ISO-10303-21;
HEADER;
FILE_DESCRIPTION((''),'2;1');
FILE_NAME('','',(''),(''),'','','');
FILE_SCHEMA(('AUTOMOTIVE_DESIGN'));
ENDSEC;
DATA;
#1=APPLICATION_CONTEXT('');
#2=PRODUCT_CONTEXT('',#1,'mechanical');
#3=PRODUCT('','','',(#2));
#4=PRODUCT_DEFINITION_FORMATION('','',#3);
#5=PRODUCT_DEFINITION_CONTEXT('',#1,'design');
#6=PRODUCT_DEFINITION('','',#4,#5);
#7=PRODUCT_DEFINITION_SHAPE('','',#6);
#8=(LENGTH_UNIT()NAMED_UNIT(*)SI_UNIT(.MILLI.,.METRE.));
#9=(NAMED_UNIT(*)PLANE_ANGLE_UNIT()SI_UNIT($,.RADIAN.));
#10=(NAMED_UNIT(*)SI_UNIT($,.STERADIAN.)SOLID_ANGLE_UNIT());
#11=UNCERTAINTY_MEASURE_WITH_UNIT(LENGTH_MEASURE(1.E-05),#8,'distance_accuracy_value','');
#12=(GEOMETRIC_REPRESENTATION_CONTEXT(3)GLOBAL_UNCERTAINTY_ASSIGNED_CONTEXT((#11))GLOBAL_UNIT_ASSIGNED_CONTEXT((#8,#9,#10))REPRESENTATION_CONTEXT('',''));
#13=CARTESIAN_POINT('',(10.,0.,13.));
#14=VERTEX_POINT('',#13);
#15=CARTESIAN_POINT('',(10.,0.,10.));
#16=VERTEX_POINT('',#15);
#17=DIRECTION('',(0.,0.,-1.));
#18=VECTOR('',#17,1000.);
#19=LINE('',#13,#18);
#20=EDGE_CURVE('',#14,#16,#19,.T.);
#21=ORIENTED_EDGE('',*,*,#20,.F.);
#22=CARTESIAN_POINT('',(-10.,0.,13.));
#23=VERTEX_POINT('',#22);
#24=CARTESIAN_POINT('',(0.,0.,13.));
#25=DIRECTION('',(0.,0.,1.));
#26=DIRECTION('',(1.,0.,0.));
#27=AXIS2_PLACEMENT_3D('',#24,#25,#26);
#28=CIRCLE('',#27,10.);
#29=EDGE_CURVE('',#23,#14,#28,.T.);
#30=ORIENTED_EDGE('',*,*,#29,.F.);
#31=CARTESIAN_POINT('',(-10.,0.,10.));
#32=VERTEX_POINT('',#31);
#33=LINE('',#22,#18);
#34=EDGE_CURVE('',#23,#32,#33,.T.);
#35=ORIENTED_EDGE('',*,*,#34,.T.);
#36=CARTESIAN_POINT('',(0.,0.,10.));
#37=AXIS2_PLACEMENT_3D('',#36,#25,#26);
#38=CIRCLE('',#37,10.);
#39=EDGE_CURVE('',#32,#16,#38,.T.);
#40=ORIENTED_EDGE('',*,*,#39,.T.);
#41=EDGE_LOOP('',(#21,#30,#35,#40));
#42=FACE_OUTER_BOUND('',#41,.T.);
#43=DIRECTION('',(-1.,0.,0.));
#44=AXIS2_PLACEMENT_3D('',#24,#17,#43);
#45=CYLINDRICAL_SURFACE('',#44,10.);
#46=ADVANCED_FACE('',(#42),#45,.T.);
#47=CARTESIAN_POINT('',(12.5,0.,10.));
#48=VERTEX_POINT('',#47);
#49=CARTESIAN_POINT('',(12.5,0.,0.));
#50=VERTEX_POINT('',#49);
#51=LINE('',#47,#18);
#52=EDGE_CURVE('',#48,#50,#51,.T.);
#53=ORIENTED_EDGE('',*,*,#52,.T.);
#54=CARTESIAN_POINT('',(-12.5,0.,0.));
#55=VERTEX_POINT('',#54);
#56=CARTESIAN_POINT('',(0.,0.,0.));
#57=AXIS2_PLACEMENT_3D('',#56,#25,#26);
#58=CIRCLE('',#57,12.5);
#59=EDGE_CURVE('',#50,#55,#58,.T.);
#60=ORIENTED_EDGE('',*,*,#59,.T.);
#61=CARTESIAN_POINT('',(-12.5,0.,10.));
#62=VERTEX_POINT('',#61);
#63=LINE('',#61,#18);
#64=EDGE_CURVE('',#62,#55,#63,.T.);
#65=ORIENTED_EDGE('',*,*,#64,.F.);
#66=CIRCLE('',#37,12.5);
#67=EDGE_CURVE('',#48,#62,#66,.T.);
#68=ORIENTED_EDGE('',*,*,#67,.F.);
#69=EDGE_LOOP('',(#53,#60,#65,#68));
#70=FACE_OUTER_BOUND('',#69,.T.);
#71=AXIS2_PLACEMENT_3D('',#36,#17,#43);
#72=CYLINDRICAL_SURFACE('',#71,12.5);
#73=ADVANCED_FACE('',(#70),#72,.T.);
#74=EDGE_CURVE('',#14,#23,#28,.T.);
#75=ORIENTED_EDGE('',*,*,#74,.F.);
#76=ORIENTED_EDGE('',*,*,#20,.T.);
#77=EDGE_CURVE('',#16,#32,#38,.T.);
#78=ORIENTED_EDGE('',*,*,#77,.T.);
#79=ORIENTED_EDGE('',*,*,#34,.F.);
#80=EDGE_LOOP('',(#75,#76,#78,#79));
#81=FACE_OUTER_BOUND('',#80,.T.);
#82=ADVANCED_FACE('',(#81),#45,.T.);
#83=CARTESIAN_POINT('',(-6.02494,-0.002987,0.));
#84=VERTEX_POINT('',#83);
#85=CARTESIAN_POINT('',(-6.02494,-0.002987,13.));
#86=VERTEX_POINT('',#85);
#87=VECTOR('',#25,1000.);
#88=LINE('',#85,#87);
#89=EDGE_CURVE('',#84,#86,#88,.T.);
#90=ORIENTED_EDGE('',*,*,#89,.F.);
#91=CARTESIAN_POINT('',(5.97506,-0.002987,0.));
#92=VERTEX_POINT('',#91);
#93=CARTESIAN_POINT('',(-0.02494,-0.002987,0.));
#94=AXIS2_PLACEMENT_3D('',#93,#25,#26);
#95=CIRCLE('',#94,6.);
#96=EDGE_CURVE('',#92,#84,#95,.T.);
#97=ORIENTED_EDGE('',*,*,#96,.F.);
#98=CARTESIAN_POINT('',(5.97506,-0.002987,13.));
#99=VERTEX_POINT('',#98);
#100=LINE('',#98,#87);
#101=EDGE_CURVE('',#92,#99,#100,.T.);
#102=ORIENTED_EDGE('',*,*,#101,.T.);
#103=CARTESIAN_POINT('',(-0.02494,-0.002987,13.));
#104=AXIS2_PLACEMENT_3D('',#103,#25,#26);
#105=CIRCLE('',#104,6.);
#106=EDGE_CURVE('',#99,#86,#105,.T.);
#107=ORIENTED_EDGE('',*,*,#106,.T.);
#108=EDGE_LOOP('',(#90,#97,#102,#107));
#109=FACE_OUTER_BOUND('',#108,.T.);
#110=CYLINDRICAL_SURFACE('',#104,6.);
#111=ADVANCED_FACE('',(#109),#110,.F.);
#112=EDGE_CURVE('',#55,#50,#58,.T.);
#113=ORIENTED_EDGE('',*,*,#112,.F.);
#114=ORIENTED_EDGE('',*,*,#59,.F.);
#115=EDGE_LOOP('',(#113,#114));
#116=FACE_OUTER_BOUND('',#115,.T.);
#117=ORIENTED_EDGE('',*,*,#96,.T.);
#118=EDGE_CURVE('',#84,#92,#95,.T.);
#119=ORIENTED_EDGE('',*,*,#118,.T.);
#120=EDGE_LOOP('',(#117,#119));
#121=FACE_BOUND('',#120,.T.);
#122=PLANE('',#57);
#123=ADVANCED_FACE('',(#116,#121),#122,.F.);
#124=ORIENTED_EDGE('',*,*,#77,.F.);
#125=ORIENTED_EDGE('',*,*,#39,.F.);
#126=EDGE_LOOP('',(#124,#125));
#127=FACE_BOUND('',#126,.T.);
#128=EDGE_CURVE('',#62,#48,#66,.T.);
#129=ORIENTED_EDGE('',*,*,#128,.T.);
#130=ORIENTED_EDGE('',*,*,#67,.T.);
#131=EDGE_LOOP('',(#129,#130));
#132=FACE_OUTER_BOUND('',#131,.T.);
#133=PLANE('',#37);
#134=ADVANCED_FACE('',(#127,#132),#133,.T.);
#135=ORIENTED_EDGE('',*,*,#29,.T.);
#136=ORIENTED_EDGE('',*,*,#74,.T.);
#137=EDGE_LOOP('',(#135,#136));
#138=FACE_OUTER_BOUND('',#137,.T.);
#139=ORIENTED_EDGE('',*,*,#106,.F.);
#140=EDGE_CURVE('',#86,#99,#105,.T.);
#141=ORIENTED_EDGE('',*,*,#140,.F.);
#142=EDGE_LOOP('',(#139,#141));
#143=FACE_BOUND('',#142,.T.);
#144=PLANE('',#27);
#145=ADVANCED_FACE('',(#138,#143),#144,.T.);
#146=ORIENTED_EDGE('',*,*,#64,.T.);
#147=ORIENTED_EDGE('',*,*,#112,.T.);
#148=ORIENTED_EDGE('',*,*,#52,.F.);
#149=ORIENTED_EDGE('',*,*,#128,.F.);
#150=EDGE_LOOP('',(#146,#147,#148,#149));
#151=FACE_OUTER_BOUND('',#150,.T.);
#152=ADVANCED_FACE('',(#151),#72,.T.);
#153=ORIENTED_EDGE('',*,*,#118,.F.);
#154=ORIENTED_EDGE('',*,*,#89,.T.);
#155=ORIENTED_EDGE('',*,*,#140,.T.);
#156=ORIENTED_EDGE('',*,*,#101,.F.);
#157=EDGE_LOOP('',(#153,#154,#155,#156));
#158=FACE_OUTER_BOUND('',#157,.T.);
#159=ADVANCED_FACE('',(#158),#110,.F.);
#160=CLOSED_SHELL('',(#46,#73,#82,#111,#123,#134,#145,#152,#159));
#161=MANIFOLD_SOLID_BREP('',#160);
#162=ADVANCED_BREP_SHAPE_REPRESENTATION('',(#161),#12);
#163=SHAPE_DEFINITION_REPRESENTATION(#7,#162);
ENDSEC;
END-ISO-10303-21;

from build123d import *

# Parameters (mm, degrees)
SKETCH1_R              = 12.5
BOSS_EXTRUDE1_DEPTH    = 10
SKETCH2_R              = 10
BOSS_EXTRUDE2_DEPTH    = 3
M14_TAPPED_HOLE1_D     = 12
M14_TAPPED_HOLE1_DEPTH = 34
M14_TAPPED_HOLE1_TIP   = 3.605163714


with BuildPart() as part:
    # Sketch1 → Boss-Extrude1 (new body)
    with BuildSketch(Plane.XY):
        Circle(SKETCH1_R)
    extrude(amount=BOSS_EXTRUDE1_DEPTH)

    # Sketch2 → Boss-Extrude2 (add)
    with BuildSketch(Plane.XY.offset(10)):
        Circle(SKETCH2_R)
    extrude(amount=BOSS_EXTRUDE2_DEPTH)

    # M14 Tapped Hole1
    with Locations(Plane(origin=(-0.024940063, -0.002986858, 13), x_dir=(1, 0, 0), z_dir=(0, 0, 1))):
        with Locations((0, 0)):
            Hole(M14_TAPPED_HOLE1_D / 2, depth=M14_TAPPED_HOLE1_DEPTH)
            with Locations((0, 0, -(M14_TAPPED_HOLE1_DEPTH + M14_TAPPED_HOLE1_TIP / 2))):  # 118° drill point
                Cone(0, M14_TAPPED_HOLE1_D / 2, M14_TAPPED_HOLE1_TIP, mode=Mode.SUBTRACT)


solid = part.part
